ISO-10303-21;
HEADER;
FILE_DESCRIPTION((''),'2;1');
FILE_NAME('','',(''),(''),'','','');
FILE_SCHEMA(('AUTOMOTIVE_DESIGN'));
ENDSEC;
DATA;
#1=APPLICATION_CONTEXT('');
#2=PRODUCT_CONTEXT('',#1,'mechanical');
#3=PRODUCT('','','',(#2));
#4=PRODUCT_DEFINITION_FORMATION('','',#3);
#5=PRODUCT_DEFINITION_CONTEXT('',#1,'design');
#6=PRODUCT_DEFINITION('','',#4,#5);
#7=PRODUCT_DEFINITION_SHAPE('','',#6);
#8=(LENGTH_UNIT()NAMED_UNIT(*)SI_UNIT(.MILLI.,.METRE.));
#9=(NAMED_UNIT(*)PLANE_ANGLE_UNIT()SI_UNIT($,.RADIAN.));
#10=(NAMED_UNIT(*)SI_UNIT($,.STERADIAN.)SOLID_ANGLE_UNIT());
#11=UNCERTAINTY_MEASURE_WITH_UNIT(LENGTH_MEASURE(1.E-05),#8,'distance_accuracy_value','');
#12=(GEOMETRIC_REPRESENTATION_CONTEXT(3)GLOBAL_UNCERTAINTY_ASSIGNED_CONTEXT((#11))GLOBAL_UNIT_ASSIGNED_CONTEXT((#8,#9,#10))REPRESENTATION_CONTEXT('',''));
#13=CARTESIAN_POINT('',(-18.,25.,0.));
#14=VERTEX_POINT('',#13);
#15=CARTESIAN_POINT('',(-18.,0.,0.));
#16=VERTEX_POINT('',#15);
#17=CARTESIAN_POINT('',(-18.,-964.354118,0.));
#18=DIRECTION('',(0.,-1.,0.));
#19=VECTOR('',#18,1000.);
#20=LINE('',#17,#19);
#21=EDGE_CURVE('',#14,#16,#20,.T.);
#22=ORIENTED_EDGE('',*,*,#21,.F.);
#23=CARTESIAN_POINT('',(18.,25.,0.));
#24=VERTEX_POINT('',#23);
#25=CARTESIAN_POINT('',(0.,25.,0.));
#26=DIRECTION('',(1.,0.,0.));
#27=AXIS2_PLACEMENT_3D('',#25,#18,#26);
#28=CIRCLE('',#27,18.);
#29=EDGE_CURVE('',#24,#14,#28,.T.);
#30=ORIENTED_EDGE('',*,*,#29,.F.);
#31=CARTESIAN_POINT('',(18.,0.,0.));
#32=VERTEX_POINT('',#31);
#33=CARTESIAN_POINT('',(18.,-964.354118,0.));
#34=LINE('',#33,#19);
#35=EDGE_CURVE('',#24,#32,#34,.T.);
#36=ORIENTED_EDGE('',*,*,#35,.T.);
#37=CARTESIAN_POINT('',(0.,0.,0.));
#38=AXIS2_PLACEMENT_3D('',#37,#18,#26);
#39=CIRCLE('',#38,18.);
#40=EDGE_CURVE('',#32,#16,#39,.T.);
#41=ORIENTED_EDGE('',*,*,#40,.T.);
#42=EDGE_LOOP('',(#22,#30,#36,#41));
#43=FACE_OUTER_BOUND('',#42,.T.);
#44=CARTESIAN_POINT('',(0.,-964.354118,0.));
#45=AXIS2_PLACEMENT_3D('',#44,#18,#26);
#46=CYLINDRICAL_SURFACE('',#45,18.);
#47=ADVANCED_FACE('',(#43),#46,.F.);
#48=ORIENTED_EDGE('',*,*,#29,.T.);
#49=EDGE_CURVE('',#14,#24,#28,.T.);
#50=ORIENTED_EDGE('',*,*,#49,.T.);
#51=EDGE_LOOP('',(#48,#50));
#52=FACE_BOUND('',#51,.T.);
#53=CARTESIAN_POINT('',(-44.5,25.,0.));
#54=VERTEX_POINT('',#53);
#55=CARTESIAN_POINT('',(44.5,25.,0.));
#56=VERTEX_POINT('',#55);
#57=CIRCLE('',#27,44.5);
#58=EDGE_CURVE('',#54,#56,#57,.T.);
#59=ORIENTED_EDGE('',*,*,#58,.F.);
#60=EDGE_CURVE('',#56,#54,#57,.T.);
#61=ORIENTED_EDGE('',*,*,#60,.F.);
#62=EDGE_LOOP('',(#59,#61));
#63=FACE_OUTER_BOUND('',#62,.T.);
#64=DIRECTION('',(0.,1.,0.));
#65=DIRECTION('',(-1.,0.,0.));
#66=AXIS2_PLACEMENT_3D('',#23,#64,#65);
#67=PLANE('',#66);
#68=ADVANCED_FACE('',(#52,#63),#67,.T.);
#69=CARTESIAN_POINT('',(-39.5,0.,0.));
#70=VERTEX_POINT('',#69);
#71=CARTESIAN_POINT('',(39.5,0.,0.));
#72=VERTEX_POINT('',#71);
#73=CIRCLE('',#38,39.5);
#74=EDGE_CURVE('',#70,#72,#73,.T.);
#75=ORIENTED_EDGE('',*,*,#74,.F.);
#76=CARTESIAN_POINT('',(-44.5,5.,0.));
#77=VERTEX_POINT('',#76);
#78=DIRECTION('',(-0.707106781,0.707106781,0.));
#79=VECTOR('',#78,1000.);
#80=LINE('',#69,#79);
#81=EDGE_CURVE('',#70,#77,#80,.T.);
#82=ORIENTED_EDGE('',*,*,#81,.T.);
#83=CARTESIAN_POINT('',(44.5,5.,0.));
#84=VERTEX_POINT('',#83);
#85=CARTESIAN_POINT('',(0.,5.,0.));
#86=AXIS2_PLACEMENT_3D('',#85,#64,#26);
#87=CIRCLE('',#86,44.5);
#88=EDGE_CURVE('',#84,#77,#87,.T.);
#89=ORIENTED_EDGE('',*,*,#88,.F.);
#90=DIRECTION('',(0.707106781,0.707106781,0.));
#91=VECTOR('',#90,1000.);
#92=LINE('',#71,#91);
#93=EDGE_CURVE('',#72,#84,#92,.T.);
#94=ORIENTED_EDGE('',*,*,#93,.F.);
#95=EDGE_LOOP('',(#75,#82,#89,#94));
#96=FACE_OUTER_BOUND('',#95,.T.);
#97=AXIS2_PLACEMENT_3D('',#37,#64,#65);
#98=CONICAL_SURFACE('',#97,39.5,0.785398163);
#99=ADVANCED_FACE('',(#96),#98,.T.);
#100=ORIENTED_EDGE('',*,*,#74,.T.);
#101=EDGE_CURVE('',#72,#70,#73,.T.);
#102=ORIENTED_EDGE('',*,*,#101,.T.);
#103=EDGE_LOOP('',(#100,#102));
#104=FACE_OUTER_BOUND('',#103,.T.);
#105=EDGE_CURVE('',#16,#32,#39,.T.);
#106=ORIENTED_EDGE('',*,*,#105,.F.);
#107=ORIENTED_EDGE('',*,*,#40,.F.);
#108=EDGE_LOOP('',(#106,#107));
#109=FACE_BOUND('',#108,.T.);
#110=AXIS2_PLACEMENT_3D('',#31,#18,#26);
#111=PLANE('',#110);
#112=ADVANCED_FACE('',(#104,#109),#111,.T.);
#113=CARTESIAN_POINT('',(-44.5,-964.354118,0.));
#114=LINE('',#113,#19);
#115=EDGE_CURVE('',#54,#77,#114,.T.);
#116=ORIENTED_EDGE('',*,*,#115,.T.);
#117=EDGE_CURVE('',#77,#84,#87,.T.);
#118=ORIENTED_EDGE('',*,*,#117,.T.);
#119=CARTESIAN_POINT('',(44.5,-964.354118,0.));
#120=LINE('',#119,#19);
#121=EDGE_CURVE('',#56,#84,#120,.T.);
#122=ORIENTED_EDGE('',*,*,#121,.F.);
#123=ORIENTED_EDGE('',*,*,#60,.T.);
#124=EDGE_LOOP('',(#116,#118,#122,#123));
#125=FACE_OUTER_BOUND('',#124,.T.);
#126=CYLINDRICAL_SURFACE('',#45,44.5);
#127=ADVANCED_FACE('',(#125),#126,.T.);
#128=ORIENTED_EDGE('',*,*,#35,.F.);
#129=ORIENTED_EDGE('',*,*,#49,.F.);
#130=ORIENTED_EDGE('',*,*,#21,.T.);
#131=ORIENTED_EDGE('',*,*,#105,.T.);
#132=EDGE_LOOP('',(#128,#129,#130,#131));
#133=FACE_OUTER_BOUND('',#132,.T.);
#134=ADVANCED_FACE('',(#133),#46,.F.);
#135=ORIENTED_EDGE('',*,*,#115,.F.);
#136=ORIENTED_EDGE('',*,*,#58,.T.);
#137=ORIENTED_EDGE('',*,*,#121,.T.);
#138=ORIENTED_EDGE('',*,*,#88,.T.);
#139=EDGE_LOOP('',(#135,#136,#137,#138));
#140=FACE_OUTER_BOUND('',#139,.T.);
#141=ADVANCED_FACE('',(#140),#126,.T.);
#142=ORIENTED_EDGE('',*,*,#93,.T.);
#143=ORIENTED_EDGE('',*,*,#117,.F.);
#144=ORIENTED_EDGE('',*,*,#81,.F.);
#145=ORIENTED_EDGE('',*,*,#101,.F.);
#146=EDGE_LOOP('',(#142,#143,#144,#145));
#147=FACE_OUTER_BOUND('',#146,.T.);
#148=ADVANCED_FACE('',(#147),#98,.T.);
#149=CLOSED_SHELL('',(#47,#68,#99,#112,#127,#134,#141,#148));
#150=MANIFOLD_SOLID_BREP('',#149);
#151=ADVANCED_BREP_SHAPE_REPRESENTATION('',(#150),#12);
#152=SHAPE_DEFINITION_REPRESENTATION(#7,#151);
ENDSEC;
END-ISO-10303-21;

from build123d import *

# Parameters (mm, degrees)
SKETCH1_W     = 26.5
SKETCH1_H     = 25
CHAMFER1_SIZE = 5


with BuildPart() as part:
    # Sketch1 → Revolve1 (revolve)
    with BuildSketch(Plane.XY):
        with Locations((31.25, 12.5)):
            Rectangle(SKETCH1_W, SKETCH1_H)
    revolve(axis=Axis((0, -964.354117897, 0), (0, 1, 0)))

    # Chamfer1
    chamfer1_edges = [part.edges().sort_by_distance(p)[0] for p in [
        (-44.5, 0, 0),
    ]]
    chamfer(chamfer1_edges, length=CHAMFER1_SIZE)


solid = part.part
